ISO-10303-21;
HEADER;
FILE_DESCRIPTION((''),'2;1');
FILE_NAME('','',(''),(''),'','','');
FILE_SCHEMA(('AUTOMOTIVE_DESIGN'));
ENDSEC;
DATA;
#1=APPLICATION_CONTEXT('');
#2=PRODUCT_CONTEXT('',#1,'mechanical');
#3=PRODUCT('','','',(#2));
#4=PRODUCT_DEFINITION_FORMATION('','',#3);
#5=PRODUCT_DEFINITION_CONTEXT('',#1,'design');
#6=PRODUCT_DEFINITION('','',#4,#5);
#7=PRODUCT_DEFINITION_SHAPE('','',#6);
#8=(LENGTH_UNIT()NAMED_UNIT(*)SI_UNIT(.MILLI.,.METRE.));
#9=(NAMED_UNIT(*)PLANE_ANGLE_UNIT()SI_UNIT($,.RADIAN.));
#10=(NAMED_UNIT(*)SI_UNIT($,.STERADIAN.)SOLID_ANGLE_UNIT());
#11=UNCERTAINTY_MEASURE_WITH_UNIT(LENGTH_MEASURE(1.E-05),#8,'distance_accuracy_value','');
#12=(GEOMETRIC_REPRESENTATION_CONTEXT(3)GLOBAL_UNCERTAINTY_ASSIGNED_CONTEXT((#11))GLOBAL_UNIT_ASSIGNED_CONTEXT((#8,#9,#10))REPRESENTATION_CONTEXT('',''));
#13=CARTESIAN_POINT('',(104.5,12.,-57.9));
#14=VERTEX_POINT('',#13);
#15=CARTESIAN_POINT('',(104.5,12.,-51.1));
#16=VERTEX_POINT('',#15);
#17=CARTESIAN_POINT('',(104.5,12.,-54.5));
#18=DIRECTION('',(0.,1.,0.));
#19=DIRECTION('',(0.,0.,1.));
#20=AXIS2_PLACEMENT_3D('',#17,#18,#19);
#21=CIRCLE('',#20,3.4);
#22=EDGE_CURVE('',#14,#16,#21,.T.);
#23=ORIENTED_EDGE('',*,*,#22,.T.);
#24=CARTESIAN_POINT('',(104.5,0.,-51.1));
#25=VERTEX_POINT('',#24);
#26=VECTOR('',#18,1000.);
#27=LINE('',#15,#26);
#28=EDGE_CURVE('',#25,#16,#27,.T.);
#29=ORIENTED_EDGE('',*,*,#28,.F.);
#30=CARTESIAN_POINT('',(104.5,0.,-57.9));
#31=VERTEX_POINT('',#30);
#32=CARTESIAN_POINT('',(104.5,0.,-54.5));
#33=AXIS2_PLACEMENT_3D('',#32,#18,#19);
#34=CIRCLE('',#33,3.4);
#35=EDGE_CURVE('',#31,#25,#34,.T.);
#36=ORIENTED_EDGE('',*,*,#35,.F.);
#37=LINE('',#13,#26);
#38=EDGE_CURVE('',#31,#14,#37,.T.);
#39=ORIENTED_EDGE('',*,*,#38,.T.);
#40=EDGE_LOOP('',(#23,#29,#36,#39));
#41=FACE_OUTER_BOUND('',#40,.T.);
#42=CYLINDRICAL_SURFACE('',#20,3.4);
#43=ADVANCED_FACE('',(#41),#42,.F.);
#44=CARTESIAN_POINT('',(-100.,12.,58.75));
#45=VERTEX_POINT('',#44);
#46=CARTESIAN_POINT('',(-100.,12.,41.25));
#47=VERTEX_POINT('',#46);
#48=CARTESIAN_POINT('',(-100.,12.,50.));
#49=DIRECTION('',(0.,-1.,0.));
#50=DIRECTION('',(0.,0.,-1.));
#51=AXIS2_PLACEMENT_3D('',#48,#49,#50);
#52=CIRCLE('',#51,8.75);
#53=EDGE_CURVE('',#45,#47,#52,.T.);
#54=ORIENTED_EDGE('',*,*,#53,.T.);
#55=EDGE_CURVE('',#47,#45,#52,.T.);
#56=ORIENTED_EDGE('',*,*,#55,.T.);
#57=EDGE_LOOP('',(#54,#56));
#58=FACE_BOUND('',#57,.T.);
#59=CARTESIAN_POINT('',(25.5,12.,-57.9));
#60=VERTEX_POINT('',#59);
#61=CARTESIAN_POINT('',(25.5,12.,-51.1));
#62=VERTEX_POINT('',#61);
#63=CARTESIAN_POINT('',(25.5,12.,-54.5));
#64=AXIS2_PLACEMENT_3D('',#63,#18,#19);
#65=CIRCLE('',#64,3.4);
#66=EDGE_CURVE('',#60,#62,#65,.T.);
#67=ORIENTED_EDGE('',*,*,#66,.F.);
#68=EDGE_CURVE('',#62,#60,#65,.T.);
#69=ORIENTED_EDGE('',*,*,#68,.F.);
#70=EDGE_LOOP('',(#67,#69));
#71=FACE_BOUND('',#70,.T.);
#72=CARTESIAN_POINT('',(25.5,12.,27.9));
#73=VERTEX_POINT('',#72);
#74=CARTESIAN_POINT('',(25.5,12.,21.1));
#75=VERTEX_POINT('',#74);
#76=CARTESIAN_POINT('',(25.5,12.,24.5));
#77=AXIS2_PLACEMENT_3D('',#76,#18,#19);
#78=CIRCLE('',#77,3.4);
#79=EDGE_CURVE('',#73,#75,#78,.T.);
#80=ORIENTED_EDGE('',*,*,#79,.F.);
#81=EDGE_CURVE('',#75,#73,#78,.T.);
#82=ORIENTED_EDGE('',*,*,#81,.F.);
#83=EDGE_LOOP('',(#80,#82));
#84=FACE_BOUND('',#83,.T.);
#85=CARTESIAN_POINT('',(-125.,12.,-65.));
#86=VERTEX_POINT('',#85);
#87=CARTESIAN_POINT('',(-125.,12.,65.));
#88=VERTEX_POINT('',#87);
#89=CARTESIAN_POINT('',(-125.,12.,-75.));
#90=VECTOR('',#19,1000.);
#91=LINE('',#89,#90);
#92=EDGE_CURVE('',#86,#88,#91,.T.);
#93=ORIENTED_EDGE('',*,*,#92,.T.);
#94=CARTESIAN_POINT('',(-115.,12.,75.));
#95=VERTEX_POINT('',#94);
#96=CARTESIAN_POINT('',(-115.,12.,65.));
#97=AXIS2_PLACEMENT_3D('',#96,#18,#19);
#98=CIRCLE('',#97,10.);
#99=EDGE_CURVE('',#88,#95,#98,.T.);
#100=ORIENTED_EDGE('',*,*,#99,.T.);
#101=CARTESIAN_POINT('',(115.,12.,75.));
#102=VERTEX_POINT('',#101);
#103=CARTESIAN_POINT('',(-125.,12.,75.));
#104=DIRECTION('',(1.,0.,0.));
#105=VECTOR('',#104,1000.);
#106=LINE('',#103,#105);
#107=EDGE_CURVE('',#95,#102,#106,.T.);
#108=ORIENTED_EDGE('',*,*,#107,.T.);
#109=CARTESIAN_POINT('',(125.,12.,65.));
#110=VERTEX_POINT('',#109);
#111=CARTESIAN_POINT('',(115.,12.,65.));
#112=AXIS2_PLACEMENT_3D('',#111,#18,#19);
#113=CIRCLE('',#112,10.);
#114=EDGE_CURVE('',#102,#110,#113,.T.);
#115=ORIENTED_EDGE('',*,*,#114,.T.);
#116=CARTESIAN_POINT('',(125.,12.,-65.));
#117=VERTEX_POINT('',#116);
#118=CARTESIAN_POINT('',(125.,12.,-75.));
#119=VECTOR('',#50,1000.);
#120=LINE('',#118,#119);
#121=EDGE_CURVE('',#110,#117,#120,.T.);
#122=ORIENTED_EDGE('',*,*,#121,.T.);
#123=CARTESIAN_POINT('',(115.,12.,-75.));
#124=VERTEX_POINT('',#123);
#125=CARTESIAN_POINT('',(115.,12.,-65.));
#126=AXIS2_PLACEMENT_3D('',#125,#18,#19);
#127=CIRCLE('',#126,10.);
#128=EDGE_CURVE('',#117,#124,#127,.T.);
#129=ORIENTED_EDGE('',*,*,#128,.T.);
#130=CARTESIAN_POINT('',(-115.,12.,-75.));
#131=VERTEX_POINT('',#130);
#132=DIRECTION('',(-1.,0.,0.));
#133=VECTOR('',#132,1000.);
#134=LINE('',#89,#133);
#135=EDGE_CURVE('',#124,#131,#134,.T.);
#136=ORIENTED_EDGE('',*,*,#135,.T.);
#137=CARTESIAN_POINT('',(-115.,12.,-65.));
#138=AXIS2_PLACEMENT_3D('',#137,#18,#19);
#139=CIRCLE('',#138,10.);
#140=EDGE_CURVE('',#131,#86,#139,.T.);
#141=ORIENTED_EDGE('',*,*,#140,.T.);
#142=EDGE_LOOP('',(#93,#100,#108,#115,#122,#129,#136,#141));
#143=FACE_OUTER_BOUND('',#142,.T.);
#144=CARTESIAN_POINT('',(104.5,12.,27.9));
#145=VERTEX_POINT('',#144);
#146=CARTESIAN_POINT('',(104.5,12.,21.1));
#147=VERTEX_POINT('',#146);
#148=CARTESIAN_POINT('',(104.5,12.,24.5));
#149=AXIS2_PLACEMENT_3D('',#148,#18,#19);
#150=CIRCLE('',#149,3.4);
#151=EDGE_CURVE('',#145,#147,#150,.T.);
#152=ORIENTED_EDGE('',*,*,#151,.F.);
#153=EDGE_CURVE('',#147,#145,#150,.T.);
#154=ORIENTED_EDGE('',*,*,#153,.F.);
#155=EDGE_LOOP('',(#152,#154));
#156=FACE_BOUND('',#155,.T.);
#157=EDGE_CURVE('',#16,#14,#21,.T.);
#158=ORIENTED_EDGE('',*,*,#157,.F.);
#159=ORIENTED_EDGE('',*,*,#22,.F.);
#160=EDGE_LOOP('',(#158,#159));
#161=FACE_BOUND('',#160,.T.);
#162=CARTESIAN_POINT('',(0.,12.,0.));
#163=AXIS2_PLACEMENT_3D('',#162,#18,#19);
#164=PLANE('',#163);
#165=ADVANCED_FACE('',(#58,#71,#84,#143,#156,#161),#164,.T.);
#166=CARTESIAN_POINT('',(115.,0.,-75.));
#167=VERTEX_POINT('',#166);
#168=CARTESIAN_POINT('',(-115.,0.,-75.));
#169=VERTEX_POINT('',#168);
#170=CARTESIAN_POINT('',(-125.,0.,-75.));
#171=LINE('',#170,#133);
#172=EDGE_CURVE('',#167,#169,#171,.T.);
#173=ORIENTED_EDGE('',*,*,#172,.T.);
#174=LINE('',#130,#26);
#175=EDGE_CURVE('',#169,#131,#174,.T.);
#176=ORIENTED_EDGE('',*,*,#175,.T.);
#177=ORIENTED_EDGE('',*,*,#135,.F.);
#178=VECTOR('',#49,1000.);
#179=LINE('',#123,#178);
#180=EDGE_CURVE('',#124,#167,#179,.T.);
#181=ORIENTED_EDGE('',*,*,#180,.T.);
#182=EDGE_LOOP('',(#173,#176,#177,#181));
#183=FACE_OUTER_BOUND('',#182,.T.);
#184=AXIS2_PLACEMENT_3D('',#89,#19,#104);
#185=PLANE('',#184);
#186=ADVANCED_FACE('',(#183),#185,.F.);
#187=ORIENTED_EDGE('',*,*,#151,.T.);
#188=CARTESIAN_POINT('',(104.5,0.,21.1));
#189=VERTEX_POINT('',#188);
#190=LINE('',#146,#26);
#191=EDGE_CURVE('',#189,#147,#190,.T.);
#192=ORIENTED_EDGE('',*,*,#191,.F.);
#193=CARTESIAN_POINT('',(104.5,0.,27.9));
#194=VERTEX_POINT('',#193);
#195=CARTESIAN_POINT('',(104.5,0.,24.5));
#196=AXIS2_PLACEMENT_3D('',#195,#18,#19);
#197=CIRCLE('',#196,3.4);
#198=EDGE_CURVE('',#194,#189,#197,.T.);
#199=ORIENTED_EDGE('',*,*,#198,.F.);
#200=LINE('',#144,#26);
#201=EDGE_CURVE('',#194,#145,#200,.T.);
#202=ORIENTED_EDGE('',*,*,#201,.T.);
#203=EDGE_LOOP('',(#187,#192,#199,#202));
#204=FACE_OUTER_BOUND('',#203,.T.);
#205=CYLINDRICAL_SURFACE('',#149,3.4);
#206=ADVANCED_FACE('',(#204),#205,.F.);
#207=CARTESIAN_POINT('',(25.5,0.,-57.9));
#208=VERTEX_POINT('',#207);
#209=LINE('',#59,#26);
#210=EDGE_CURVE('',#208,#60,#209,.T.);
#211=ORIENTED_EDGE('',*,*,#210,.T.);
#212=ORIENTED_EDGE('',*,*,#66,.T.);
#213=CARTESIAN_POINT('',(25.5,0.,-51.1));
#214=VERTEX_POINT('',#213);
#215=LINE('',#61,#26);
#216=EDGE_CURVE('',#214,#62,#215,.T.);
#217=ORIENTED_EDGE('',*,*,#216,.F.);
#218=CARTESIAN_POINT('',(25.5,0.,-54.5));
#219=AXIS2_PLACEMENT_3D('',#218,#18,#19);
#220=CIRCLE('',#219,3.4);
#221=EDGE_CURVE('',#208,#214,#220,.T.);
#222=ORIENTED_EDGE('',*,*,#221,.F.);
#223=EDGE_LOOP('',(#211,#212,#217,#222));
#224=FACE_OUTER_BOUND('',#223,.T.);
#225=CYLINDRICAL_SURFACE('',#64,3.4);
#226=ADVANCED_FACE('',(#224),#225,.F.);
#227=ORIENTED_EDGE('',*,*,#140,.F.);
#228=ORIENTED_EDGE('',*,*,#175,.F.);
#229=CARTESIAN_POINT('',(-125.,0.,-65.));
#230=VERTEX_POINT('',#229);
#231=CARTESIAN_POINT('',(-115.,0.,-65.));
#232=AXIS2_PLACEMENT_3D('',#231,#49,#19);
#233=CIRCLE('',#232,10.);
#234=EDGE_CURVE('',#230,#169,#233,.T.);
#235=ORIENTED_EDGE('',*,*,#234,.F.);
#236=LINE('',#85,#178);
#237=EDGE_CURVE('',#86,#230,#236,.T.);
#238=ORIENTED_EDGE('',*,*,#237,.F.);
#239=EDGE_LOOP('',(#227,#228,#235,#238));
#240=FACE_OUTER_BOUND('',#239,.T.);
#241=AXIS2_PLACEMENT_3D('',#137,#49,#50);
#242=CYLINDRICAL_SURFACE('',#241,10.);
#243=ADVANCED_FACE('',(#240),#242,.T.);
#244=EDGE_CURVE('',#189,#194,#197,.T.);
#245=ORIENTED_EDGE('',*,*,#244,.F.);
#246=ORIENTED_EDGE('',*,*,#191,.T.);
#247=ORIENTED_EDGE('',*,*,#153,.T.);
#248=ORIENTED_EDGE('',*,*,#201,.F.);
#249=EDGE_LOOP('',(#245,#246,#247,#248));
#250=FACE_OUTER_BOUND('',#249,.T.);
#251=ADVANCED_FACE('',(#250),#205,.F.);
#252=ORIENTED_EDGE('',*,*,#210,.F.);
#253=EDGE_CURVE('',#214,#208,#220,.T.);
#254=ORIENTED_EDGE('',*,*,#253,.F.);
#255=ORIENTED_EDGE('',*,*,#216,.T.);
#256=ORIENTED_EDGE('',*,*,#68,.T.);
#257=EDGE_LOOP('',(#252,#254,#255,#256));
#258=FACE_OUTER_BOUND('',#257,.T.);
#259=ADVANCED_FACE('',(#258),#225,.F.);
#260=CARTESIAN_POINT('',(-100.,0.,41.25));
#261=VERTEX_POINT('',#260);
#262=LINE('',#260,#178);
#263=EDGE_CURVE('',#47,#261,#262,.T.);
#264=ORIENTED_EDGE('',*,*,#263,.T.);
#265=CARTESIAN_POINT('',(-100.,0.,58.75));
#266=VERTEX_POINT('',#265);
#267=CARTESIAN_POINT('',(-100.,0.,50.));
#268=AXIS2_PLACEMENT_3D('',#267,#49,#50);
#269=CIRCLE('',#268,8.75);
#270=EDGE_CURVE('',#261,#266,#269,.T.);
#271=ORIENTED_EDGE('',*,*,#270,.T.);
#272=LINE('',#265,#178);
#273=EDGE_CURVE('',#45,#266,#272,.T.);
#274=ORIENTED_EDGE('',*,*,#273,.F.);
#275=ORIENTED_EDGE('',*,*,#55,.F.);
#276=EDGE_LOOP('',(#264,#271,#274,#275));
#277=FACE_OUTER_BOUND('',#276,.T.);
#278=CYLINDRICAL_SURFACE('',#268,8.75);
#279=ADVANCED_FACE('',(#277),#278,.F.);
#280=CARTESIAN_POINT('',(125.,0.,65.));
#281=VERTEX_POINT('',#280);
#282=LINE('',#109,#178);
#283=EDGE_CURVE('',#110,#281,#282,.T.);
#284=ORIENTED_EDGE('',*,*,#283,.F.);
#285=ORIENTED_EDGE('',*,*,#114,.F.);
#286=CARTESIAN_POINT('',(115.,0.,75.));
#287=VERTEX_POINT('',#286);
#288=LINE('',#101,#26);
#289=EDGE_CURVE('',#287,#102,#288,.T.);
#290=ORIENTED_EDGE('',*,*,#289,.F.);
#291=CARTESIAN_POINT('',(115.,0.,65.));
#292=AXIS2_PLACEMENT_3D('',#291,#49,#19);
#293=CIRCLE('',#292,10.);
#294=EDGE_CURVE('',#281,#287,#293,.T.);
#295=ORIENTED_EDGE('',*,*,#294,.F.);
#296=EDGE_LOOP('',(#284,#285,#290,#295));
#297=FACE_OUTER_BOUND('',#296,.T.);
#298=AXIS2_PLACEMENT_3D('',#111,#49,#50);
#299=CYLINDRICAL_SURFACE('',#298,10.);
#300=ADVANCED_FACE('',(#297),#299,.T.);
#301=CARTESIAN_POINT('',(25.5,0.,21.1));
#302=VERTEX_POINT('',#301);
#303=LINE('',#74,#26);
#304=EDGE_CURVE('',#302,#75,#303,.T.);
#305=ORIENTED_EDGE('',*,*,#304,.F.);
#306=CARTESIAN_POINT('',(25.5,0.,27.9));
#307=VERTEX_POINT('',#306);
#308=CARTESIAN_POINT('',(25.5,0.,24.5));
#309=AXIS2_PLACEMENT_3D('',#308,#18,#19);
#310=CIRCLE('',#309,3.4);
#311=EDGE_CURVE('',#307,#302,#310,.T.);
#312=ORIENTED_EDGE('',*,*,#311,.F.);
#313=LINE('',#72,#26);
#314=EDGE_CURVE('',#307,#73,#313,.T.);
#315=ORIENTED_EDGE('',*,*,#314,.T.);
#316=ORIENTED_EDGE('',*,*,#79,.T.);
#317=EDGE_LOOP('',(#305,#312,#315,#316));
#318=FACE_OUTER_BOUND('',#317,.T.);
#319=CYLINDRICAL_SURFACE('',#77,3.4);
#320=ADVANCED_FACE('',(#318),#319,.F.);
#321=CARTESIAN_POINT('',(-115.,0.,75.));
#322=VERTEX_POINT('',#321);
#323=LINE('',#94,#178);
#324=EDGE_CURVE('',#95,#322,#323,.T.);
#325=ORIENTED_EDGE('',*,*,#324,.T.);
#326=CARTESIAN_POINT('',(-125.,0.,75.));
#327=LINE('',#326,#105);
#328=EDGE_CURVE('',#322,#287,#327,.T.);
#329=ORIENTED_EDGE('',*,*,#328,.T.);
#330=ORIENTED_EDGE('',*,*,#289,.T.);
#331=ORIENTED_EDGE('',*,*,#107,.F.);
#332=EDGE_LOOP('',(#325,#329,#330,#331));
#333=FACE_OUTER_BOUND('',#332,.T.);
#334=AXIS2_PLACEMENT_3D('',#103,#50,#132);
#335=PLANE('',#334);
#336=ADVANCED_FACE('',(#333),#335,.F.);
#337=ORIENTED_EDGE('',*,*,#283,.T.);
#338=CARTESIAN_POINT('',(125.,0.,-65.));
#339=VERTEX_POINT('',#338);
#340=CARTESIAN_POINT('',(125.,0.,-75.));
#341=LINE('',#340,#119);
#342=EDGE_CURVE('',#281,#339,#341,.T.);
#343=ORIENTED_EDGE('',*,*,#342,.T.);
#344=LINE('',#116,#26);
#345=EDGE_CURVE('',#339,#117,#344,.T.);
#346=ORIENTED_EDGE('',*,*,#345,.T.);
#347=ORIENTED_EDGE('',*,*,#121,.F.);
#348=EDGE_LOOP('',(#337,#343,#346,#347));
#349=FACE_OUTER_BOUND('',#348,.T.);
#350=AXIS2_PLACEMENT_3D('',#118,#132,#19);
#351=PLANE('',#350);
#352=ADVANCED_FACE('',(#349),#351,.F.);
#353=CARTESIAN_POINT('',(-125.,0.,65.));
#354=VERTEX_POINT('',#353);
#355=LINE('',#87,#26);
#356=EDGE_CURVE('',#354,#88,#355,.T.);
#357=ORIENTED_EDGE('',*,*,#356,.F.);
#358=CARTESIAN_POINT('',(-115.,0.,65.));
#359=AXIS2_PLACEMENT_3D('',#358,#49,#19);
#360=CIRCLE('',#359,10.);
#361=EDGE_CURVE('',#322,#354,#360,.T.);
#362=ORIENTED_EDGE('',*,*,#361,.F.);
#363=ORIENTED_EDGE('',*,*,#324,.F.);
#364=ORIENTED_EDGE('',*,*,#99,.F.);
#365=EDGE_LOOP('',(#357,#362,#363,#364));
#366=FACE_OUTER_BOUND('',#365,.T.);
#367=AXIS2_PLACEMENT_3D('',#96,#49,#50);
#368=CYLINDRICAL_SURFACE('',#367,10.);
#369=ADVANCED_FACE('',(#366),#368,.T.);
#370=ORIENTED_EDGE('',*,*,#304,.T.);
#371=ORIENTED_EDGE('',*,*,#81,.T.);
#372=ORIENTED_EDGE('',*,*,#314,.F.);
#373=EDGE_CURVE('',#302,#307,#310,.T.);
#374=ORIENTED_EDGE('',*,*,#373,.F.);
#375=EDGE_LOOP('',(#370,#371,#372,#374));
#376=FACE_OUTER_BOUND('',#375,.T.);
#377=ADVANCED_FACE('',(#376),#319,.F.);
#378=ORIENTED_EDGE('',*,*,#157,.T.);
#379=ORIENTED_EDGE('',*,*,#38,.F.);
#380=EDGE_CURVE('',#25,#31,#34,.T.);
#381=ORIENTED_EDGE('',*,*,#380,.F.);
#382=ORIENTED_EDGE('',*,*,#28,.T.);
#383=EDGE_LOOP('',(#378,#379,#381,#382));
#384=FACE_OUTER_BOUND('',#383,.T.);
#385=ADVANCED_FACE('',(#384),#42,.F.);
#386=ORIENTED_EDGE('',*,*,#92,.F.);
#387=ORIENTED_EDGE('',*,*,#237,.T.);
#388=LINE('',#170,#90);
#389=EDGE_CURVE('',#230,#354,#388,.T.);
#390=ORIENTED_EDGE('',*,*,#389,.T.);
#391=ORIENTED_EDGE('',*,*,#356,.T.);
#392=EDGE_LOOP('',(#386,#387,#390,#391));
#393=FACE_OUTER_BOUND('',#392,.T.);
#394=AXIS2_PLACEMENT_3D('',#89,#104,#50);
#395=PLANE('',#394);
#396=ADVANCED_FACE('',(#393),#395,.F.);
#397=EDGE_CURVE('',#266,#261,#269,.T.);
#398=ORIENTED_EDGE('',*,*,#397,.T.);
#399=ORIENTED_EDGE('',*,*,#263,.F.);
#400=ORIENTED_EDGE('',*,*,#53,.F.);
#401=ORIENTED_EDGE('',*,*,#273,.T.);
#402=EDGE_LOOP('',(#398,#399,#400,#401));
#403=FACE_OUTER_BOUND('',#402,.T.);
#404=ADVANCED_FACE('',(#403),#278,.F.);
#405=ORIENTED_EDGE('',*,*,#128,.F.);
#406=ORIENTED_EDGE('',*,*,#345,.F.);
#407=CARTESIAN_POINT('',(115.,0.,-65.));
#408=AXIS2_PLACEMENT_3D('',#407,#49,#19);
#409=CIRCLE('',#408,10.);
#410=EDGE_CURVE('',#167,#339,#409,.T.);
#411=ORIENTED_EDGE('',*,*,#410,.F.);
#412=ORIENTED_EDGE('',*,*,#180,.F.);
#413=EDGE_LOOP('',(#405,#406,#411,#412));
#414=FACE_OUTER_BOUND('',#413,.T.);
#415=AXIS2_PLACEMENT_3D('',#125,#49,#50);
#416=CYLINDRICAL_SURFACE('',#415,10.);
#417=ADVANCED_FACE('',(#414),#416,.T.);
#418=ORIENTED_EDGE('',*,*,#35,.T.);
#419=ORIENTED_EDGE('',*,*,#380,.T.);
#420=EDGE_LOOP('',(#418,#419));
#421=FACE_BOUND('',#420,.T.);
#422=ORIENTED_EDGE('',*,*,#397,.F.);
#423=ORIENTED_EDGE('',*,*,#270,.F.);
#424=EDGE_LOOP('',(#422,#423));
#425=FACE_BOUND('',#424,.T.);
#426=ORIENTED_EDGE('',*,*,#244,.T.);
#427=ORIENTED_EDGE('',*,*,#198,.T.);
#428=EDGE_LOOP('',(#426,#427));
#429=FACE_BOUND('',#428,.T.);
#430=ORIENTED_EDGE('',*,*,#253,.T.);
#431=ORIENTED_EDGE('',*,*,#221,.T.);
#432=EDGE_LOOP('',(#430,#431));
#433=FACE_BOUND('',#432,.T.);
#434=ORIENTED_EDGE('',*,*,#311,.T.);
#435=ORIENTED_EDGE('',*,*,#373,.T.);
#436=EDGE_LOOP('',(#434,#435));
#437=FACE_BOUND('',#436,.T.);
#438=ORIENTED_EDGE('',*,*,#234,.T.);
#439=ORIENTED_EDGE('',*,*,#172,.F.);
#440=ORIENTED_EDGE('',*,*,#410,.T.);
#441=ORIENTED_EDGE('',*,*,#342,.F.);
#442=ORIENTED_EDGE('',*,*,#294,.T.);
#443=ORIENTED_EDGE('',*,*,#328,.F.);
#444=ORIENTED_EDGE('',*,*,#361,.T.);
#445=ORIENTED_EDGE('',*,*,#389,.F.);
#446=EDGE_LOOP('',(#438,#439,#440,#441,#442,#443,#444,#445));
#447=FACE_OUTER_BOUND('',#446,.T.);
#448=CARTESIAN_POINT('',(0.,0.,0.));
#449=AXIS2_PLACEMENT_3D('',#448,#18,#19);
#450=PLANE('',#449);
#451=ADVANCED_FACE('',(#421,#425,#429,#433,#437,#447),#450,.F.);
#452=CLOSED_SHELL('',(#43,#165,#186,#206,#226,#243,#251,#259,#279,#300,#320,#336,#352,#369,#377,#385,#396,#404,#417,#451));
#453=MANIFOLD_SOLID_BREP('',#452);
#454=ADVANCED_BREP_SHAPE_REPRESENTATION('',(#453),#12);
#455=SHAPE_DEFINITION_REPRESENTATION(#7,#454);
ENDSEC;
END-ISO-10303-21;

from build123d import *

# Parameters (mm, degrees)
SKETCH_1_W          = 250
SKETCH_1_H          = 150
EXTRUDE_1_DEPTH     = 12
HOLE_WIZARD_M20_1_D = 17.5
HOLE_WIZARD_M8_1_D  = 6.8
FILLET_1_R          = 10


with BuildPart() as part:
    # 草图1 → 凸台-拉伸1 (new body)
    with BuildSketch(Plane(origin=(0, 0, 0), x_dir=(1, 0, 0), z_dir=(0, 1, 0))):
        Rectangle(SKETCH_1_W, SKETCH_1_H)
    extrude(amount=EXTRUDE_1_DEPTH)

    # M20 螺纹孔1 (through all)
    with Locations(Plane(origin=(0, 0, 0), x_dir=(-1, 0, 0), z_dir=(0, -1, 0))):
        with Locations((100, -50)):
            Hole(HOLE_WIZARD_M20_1_D / 2)

    # M8 螺纹孔1 (through all)
    with Locations(Plane(origin=(0, 12, 0), x_dir=(1, 0, 0), z_dir=(0, 1, 0))):
        with Locations((25.5, 54.5), (104.5, 54.5), (25.5, -24.5), (104.5, -24.5)):
            Hole(HOLE_WIZARD_M8_1_D / 2)

    # 圆角1
    fillet_1_edges = [part.edges().sort_by_distance(p)[0] for p in [
        (125, 6, 75),
        (-125, 6, 75),
        (-125, 6, -75),
        (125, 6, -75),
    ]]
    fillet(fillet_1_edges, radius=FILLET_1_R)


solid = part.part
